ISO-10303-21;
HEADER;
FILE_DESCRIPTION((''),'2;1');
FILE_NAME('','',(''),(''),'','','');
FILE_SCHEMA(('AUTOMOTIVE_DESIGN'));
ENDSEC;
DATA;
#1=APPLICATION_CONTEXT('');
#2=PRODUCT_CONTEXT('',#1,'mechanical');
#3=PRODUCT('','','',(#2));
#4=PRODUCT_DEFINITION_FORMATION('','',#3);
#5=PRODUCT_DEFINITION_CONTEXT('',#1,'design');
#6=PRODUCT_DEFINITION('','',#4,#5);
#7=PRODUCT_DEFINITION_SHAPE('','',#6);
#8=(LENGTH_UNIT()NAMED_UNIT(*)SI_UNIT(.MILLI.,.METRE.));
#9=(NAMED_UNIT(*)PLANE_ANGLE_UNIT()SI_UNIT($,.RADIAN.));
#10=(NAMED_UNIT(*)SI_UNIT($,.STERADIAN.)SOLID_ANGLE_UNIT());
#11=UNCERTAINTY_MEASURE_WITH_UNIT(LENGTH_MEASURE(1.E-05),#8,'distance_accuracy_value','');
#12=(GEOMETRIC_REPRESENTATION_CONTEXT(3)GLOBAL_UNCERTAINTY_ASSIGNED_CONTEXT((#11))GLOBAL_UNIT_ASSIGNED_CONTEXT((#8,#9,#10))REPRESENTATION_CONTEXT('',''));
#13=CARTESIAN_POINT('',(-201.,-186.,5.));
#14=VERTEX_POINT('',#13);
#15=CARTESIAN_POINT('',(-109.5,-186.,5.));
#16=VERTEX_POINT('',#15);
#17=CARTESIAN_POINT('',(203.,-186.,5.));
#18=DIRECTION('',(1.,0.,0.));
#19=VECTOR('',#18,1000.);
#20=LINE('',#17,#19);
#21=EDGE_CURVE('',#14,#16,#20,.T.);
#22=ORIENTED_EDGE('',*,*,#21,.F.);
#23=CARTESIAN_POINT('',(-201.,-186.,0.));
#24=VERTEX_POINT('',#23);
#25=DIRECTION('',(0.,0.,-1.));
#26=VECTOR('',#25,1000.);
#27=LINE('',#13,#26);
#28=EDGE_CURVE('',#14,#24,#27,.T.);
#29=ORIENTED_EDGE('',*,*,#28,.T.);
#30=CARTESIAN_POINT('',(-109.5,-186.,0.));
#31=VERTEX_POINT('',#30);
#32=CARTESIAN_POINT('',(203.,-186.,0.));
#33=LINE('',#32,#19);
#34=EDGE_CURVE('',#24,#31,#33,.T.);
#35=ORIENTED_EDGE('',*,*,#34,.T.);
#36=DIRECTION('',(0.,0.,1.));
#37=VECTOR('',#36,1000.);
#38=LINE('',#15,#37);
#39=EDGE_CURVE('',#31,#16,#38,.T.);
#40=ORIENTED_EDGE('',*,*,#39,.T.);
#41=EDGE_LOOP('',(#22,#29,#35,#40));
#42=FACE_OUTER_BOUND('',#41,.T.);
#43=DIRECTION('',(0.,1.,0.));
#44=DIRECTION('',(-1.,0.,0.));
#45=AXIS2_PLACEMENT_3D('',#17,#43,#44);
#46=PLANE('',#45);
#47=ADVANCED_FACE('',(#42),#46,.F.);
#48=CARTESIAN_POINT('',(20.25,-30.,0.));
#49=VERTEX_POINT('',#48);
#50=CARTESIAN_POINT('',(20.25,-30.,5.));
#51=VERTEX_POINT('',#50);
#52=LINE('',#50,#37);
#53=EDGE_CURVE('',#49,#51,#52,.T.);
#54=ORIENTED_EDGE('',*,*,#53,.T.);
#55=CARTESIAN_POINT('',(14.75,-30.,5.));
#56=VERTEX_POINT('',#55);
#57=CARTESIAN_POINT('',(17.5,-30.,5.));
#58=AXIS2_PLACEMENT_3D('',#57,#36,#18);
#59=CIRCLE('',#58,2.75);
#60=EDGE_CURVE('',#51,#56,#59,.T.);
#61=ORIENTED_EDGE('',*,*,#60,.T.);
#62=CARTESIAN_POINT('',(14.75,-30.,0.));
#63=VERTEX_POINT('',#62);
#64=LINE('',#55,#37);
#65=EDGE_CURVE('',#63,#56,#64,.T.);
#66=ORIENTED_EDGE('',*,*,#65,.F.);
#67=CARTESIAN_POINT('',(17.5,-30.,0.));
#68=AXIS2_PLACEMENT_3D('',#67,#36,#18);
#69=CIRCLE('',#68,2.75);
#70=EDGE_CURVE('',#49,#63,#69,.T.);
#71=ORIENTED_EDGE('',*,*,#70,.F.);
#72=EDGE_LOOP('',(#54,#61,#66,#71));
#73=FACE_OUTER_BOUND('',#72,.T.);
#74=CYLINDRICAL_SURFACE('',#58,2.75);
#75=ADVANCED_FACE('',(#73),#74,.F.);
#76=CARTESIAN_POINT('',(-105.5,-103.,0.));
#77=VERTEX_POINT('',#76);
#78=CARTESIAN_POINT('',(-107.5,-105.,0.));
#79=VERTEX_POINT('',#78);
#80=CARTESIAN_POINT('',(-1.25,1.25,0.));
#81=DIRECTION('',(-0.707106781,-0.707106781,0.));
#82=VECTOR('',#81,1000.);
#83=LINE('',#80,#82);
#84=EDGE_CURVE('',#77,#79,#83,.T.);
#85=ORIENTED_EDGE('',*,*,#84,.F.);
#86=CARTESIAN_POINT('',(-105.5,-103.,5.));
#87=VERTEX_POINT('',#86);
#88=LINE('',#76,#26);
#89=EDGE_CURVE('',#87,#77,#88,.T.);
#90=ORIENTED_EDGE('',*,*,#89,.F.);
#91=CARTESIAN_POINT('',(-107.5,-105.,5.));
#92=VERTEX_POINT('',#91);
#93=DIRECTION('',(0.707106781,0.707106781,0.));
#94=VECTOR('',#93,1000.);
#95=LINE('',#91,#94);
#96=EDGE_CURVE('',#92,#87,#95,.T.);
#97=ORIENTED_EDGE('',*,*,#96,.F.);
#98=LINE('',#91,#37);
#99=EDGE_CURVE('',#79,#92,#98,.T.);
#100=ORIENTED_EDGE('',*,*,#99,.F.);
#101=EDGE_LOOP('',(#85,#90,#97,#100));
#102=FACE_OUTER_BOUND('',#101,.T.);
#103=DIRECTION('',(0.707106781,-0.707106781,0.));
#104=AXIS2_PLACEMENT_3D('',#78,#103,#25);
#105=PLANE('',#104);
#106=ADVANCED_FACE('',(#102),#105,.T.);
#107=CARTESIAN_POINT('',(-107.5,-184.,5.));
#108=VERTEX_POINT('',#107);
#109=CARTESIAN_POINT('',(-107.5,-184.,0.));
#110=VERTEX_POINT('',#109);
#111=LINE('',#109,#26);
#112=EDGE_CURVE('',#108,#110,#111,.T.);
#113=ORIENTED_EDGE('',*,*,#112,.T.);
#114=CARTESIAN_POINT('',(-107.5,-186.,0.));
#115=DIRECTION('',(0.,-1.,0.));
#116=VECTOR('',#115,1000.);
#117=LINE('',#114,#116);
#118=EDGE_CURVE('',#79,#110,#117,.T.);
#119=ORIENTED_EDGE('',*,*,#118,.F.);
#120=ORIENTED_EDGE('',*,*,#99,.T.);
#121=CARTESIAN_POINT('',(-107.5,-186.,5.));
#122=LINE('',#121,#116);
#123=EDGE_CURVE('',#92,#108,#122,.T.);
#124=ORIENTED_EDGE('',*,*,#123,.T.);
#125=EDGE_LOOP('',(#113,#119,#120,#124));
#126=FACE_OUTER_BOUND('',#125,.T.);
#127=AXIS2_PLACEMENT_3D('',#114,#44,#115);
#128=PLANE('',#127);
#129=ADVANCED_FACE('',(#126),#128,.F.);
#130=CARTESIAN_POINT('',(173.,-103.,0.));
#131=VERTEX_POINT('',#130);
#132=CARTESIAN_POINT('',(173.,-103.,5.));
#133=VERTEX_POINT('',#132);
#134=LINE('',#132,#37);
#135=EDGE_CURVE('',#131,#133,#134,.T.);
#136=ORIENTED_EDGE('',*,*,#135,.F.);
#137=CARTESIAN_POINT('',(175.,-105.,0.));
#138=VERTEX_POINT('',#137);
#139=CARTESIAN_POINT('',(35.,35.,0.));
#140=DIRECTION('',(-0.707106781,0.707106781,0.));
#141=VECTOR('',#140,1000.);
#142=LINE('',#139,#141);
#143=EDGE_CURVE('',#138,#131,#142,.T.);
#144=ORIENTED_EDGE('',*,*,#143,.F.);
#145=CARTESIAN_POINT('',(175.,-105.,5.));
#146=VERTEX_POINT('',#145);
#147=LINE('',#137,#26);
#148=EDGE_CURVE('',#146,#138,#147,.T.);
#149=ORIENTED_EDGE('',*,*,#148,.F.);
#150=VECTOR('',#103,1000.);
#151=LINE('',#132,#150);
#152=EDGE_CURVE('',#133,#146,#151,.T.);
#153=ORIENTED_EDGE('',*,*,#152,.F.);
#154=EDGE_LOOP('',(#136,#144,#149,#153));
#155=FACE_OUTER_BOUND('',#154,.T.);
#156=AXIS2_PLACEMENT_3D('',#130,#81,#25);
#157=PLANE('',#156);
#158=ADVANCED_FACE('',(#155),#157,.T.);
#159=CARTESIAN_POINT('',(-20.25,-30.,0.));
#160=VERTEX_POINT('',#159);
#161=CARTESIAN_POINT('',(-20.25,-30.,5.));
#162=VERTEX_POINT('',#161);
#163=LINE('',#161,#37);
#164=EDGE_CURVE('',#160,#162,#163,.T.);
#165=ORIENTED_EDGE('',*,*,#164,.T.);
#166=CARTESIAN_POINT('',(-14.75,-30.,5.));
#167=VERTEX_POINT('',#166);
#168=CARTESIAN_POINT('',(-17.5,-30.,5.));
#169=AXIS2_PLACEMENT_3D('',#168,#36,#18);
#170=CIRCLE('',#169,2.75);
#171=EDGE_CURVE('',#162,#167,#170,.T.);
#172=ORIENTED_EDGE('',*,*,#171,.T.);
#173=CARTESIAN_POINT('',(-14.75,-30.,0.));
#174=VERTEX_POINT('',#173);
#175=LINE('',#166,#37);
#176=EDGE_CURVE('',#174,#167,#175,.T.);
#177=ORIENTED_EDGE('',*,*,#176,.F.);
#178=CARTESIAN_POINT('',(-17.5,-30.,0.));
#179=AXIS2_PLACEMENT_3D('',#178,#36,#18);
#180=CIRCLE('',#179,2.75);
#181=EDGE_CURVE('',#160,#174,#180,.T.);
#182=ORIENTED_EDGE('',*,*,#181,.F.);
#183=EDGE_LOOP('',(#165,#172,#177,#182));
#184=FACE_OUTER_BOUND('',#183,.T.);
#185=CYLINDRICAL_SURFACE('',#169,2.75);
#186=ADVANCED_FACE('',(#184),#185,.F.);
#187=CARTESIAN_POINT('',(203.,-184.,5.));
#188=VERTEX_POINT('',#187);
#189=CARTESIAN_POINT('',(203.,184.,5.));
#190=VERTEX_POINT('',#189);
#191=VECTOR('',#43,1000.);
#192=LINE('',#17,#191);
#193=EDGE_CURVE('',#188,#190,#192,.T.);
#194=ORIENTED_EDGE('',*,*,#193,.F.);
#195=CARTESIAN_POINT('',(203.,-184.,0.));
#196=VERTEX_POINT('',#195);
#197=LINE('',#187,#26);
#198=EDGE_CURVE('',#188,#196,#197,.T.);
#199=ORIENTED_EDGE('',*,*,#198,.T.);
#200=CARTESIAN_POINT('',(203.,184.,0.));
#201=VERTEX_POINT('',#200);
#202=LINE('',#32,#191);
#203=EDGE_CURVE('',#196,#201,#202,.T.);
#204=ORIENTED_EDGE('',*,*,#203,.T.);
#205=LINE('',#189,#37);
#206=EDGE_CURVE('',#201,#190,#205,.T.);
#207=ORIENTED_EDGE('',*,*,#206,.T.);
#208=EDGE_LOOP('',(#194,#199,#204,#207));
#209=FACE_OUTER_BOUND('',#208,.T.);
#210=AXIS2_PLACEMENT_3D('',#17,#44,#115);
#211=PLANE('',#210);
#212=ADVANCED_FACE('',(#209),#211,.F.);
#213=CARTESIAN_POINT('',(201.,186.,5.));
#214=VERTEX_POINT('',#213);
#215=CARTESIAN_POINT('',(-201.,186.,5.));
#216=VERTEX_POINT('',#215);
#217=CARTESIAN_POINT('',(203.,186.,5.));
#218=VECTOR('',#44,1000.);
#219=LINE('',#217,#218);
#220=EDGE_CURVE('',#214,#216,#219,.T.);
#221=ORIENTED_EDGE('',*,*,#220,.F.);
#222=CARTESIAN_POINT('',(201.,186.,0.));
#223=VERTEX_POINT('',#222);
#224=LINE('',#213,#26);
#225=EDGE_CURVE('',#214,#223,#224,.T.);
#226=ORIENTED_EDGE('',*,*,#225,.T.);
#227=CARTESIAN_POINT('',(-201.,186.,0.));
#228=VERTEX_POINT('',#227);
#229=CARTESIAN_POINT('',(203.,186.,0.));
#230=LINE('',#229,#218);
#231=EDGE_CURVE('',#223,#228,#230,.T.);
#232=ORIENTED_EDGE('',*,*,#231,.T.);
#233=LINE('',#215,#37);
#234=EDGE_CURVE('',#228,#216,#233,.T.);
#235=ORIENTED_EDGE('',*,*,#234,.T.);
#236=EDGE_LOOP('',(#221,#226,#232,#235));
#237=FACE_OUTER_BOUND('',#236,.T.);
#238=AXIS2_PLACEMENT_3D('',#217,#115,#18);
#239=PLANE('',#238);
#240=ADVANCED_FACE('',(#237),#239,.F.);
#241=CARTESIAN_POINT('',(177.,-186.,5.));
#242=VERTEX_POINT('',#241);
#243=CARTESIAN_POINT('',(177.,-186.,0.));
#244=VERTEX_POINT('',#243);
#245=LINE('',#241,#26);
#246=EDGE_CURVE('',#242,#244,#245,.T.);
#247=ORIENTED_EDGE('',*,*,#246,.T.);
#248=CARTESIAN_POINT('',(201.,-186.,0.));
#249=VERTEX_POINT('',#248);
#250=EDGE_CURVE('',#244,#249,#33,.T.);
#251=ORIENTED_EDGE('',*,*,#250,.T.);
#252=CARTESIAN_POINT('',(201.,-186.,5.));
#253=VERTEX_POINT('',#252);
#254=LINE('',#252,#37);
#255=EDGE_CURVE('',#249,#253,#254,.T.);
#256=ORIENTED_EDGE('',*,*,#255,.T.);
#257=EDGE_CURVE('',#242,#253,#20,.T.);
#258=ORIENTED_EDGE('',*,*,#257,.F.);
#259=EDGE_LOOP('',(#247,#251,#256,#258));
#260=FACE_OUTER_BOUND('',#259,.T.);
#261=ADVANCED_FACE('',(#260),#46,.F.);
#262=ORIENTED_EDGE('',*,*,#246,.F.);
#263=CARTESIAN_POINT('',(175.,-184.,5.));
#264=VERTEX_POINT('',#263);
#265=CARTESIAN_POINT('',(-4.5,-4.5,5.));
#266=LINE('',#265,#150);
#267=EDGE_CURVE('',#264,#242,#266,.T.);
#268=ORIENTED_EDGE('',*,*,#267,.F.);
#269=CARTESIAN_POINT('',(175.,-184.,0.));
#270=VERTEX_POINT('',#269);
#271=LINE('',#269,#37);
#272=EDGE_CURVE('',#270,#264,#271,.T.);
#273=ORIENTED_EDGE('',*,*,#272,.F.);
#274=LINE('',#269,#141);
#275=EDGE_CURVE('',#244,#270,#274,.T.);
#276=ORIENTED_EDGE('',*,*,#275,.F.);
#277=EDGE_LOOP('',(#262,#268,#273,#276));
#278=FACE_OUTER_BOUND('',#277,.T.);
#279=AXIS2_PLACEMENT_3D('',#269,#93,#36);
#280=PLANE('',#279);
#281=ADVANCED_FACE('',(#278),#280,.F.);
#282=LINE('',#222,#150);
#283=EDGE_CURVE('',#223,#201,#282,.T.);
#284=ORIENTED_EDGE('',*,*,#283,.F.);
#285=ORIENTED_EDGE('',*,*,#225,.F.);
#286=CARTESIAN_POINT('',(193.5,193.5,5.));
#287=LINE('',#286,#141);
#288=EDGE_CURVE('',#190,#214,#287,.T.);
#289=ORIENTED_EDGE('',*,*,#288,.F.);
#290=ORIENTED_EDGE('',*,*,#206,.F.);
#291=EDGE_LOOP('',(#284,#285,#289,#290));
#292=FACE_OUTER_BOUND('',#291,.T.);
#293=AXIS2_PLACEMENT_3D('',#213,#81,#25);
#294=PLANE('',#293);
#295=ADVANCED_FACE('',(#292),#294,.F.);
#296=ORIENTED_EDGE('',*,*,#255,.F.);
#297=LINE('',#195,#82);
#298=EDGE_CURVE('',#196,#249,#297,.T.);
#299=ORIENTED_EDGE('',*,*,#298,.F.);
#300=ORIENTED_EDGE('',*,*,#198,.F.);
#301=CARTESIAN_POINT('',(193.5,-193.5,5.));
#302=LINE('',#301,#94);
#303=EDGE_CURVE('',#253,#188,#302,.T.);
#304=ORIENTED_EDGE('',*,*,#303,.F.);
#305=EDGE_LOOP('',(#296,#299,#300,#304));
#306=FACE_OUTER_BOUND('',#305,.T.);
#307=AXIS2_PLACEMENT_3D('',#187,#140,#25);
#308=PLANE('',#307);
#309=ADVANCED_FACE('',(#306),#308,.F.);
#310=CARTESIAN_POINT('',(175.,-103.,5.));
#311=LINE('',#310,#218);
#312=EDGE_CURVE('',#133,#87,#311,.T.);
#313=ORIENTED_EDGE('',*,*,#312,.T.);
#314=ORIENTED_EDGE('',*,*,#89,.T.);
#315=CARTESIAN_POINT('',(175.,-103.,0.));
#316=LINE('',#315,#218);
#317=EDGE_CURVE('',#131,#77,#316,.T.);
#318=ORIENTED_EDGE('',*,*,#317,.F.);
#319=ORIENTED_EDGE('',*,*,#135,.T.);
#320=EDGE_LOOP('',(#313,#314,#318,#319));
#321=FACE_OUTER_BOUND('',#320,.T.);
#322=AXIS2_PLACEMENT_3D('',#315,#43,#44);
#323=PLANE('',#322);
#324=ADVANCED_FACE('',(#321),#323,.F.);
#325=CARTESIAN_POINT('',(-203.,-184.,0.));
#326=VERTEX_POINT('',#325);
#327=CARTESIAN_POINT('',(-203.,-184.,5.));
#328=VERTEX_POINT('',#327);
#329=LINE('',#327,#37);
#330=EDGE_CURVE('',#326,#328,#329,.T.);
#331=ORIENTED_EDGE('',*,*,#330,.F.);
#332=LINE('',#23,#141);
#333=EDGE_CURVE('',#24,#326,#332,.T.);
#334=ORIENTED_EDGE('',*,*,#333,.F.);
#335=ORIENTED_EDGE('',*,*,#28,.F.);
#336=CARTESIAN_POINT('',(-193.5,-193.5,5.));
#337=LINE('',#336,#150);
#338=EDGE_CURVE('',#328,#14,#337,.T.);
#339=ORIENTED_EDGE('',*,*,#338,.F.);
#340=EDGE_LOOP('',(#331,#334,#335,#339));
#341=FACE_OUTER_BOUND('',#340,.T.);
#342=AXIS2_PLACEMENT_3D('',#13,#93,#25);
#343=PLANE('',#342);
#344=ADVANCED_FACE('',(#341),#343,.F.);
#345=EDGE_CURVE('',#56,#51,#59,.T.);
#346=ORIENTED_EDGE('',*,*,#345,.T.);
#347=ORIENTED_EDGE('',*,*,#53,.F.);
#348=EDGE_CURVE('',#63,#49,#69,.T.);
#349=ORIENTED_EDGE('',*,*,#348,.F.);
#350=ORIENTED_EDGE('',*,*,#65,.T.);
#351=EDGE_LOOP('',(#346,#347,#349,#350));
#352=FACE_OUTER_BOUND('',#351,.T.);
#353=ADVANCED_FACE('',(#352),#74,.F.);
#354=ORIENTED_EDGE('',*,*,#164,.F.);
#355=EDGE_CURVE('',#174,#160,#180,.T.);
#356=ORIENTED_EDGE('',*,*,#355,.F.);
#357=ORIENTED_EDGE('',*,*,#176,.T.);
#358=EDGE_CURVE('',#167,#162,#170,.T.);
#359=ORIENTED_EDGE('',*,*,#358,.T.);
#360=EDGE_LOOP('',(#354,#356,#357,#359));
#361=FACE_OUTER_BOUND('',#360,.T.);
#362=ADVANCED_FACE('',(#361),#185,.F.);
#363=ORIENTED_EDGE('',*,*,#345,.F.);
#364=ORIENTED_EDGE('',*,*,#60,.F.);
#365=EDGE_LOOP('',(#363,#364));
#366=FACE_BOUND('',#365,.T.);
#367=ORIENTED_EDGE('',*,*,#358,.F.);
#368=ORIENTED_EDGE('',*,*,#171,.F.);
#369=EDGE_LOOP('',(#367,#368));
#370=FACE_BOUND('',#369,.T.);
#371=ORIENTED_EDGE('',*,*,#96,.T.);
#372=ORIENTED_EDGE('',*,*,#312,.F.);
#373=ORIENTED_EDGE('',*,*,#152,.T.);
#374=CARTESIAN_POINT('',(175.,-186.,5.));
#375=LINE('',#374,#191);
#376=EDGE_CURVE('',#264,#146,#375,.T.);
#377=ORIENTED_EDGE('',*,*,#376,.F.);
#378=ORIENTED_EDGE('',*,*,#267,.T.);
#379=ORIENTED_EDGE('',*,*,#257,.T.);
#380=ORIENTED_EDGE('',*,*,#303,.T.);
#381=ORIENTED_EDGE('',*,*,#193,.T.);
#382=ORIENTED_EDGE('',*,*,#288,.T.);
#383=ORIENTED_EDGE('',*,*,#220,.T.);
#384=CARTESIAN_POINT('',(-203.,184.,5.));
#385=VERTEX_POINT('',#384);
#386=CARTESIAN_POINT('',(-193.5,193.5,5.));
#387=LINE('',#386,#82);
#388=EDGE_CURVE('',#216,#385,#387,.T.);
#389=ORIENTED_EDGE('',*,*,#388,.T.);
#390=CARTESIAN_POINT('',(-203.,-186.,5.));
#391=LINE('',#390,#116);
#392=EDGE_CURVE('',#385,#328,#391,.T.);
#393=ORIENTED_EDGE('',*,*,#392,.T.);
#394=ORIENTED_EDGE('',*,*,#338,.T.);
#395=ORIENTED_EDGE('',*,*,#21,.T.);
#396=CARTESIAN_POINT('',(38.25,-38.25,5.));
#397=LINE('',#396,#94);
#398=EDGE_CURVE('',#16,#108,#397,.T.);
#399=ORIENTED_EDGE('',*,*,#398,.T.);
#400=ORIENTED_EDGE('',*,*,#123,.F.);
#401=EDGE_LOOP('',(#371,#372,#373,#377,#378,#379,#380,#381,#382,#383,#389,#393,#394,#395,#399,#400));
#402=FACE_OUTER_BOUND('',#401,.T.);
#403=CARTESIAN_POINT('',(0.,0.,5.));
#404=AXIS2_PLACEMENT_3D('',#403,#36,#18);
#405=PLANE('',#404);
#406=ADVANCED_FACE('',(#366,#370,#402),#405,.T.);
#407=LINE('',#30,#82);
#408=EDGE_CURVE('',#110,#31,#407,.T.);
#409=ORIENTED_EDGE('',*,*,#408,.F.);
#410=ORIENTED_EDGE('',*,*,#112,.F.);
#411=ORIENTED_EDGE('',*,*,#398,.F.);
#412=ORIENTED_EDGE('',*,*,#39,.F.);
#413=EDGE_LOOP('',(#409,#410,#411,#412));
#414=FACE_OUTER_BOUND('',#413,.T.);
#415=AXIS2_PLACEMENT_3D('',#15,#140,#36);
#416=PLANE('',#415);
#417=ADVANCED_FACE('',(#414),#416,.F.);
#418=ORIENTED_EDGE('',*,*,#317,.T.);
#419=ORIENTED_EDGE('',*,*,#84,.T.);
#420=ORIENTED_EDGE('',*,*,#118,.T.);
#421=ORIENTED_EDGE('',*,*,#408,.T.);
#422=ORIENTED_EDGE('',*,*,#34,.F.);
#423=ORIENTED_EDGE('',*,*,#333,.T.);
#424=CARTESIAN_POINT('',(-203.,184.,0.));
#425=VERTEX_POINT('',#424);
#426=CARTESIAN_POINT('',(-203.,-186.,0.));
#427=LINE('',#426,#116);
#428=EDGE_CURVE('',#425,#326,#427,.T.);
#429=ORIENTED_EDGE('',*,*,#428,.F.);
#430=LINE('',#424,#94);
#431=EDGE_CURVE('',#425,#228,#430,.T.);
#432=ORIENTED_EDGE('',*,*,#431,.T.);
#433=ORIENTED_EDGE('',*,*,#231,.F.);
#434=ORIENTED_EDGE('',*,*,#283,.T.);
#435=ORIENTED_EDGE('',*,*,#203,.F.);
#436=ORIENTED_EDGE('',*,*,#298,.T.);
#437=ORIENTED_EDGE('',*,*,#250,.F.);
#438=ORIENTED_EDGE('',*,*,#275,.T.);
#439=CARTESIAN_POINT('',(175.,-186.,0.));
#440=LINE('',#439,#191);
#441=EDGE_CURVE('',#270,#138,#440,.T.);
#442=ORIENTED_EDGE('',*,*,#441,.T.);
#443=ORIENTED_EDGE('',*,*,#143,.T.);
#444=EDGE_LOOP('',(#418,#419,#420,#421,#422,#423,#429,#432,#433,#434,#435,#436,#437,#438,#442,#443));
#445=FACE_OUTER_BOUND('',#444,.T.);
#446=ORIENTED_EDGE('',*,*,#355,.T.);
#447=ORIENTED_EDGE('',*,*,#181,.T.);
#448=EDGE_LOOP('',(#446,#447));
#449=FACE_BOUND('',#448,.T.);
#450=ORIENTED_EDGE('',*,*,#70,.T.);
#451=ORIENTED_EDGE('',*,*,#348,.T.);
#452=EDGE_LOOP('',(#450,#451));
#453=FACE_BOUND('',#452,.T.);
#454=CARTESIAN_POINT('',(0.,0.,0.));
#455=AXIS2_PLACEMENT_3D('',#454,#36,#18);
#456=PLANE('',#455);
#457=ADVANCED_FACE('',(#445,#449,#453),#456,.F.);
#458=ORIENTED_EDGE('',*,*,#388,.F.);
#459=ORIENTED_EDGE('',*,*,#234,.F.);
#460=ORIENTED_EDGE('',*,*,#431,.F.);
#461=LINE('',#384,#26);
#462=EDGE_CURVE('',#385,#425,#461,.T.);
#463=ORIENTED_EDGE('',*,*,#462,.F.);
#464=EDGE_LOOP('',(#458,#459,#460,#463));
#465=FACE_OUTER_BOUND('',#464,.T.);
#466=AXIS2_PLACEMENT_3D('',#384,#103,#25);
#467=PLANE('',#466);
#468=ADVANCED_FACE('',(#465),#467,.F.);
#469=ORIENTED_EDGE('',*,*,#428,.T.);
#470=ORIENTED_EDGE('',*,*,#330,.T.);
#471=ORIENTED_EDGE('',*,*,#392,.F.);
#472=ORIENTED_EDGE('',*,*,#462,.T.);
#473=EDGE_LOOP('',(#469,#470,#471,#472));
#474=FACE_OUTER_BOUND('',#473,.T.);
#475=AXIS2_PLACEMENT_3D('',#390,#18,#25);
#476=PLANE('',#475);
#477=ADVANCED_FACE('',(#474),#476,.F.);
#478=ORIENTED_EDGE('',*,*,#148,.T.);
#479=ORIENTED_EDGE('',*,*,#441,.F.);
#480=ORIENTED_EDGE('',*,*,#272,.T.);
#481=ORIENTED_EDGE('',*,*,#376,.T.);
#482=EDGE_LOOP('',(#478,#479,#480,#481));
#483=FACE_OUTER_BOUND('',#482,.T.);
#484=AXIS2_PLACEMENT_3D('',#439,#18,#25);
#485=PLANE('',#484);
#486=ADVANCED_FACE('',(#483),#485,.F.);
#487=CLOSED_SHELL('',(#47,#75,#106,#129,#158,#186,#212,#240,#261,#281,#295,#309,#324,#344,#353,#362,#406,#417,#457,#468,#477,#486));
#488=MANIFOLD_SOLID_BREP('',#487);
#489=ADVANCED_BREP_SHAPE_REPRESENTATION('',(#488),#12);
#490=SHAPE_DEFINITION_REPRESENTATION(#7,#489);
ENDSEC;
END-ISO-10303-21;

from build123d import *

# Parameters (mm, degrees)
SKETCH1_W            = 406
SKETCH1_H            = 372
BOSS_EXTRUDE1_DEPTH  = 5
SKETCH2_W            = 282.5
SKETCH2_H            = 83
CUT_EXTRUDE1_DEPTH   = 276.372475022
M5_CLEARANCE_HOLE1_D = 5.5
FILLET1_SIZE         = 2


with BuildPart() as part:
    # Sketch1 → Boss-Extrude1 (new body)
    with BuildSketch(Plane.XY):
        Rectangle(SKETCH1_W, SKETCH1_H)
    extrude(amount=BOSS_EXTRUDE1_DEPTH)

    # Sketch2 → Cut-Extrude1 (cut, through all)
    with BuildSketch(Plane.XY.offset(5)):
        with Locations((33.75, -144.5)):
            Rectangle(SKETCH2_W, SKETCH2_H)
    extrude(amount=-CUT_EXTRUDE1_DEPTH, mode=Mode.SUBTRACT)

    # M5 Clearance Hole1 (through all)
    with Locations(Plane.XY.offset(5)):
        with Locations((-17.5, -30), (17.5, -30)):
            Hole(M5_CLEARANCE_HOLE1_D / 2)

    # Fillet1
    fillet1_edges = [part.edges().sort_by_distance(p)[0] for p in [
        (-107.5, -186, 2.5),
        (-107.5, -103, 2.5),
        (175, -103, 2.5),
        (175, -186, 2.5),
        (-203, 186, 2.5),
        (203, 186, 2.5),
        (203, -186, 2.5),
        (-203, -186, 2.5),
    ]]
    chamfer(fillet1_edges, length=FILLET1_SIZE)


solid = part.part
